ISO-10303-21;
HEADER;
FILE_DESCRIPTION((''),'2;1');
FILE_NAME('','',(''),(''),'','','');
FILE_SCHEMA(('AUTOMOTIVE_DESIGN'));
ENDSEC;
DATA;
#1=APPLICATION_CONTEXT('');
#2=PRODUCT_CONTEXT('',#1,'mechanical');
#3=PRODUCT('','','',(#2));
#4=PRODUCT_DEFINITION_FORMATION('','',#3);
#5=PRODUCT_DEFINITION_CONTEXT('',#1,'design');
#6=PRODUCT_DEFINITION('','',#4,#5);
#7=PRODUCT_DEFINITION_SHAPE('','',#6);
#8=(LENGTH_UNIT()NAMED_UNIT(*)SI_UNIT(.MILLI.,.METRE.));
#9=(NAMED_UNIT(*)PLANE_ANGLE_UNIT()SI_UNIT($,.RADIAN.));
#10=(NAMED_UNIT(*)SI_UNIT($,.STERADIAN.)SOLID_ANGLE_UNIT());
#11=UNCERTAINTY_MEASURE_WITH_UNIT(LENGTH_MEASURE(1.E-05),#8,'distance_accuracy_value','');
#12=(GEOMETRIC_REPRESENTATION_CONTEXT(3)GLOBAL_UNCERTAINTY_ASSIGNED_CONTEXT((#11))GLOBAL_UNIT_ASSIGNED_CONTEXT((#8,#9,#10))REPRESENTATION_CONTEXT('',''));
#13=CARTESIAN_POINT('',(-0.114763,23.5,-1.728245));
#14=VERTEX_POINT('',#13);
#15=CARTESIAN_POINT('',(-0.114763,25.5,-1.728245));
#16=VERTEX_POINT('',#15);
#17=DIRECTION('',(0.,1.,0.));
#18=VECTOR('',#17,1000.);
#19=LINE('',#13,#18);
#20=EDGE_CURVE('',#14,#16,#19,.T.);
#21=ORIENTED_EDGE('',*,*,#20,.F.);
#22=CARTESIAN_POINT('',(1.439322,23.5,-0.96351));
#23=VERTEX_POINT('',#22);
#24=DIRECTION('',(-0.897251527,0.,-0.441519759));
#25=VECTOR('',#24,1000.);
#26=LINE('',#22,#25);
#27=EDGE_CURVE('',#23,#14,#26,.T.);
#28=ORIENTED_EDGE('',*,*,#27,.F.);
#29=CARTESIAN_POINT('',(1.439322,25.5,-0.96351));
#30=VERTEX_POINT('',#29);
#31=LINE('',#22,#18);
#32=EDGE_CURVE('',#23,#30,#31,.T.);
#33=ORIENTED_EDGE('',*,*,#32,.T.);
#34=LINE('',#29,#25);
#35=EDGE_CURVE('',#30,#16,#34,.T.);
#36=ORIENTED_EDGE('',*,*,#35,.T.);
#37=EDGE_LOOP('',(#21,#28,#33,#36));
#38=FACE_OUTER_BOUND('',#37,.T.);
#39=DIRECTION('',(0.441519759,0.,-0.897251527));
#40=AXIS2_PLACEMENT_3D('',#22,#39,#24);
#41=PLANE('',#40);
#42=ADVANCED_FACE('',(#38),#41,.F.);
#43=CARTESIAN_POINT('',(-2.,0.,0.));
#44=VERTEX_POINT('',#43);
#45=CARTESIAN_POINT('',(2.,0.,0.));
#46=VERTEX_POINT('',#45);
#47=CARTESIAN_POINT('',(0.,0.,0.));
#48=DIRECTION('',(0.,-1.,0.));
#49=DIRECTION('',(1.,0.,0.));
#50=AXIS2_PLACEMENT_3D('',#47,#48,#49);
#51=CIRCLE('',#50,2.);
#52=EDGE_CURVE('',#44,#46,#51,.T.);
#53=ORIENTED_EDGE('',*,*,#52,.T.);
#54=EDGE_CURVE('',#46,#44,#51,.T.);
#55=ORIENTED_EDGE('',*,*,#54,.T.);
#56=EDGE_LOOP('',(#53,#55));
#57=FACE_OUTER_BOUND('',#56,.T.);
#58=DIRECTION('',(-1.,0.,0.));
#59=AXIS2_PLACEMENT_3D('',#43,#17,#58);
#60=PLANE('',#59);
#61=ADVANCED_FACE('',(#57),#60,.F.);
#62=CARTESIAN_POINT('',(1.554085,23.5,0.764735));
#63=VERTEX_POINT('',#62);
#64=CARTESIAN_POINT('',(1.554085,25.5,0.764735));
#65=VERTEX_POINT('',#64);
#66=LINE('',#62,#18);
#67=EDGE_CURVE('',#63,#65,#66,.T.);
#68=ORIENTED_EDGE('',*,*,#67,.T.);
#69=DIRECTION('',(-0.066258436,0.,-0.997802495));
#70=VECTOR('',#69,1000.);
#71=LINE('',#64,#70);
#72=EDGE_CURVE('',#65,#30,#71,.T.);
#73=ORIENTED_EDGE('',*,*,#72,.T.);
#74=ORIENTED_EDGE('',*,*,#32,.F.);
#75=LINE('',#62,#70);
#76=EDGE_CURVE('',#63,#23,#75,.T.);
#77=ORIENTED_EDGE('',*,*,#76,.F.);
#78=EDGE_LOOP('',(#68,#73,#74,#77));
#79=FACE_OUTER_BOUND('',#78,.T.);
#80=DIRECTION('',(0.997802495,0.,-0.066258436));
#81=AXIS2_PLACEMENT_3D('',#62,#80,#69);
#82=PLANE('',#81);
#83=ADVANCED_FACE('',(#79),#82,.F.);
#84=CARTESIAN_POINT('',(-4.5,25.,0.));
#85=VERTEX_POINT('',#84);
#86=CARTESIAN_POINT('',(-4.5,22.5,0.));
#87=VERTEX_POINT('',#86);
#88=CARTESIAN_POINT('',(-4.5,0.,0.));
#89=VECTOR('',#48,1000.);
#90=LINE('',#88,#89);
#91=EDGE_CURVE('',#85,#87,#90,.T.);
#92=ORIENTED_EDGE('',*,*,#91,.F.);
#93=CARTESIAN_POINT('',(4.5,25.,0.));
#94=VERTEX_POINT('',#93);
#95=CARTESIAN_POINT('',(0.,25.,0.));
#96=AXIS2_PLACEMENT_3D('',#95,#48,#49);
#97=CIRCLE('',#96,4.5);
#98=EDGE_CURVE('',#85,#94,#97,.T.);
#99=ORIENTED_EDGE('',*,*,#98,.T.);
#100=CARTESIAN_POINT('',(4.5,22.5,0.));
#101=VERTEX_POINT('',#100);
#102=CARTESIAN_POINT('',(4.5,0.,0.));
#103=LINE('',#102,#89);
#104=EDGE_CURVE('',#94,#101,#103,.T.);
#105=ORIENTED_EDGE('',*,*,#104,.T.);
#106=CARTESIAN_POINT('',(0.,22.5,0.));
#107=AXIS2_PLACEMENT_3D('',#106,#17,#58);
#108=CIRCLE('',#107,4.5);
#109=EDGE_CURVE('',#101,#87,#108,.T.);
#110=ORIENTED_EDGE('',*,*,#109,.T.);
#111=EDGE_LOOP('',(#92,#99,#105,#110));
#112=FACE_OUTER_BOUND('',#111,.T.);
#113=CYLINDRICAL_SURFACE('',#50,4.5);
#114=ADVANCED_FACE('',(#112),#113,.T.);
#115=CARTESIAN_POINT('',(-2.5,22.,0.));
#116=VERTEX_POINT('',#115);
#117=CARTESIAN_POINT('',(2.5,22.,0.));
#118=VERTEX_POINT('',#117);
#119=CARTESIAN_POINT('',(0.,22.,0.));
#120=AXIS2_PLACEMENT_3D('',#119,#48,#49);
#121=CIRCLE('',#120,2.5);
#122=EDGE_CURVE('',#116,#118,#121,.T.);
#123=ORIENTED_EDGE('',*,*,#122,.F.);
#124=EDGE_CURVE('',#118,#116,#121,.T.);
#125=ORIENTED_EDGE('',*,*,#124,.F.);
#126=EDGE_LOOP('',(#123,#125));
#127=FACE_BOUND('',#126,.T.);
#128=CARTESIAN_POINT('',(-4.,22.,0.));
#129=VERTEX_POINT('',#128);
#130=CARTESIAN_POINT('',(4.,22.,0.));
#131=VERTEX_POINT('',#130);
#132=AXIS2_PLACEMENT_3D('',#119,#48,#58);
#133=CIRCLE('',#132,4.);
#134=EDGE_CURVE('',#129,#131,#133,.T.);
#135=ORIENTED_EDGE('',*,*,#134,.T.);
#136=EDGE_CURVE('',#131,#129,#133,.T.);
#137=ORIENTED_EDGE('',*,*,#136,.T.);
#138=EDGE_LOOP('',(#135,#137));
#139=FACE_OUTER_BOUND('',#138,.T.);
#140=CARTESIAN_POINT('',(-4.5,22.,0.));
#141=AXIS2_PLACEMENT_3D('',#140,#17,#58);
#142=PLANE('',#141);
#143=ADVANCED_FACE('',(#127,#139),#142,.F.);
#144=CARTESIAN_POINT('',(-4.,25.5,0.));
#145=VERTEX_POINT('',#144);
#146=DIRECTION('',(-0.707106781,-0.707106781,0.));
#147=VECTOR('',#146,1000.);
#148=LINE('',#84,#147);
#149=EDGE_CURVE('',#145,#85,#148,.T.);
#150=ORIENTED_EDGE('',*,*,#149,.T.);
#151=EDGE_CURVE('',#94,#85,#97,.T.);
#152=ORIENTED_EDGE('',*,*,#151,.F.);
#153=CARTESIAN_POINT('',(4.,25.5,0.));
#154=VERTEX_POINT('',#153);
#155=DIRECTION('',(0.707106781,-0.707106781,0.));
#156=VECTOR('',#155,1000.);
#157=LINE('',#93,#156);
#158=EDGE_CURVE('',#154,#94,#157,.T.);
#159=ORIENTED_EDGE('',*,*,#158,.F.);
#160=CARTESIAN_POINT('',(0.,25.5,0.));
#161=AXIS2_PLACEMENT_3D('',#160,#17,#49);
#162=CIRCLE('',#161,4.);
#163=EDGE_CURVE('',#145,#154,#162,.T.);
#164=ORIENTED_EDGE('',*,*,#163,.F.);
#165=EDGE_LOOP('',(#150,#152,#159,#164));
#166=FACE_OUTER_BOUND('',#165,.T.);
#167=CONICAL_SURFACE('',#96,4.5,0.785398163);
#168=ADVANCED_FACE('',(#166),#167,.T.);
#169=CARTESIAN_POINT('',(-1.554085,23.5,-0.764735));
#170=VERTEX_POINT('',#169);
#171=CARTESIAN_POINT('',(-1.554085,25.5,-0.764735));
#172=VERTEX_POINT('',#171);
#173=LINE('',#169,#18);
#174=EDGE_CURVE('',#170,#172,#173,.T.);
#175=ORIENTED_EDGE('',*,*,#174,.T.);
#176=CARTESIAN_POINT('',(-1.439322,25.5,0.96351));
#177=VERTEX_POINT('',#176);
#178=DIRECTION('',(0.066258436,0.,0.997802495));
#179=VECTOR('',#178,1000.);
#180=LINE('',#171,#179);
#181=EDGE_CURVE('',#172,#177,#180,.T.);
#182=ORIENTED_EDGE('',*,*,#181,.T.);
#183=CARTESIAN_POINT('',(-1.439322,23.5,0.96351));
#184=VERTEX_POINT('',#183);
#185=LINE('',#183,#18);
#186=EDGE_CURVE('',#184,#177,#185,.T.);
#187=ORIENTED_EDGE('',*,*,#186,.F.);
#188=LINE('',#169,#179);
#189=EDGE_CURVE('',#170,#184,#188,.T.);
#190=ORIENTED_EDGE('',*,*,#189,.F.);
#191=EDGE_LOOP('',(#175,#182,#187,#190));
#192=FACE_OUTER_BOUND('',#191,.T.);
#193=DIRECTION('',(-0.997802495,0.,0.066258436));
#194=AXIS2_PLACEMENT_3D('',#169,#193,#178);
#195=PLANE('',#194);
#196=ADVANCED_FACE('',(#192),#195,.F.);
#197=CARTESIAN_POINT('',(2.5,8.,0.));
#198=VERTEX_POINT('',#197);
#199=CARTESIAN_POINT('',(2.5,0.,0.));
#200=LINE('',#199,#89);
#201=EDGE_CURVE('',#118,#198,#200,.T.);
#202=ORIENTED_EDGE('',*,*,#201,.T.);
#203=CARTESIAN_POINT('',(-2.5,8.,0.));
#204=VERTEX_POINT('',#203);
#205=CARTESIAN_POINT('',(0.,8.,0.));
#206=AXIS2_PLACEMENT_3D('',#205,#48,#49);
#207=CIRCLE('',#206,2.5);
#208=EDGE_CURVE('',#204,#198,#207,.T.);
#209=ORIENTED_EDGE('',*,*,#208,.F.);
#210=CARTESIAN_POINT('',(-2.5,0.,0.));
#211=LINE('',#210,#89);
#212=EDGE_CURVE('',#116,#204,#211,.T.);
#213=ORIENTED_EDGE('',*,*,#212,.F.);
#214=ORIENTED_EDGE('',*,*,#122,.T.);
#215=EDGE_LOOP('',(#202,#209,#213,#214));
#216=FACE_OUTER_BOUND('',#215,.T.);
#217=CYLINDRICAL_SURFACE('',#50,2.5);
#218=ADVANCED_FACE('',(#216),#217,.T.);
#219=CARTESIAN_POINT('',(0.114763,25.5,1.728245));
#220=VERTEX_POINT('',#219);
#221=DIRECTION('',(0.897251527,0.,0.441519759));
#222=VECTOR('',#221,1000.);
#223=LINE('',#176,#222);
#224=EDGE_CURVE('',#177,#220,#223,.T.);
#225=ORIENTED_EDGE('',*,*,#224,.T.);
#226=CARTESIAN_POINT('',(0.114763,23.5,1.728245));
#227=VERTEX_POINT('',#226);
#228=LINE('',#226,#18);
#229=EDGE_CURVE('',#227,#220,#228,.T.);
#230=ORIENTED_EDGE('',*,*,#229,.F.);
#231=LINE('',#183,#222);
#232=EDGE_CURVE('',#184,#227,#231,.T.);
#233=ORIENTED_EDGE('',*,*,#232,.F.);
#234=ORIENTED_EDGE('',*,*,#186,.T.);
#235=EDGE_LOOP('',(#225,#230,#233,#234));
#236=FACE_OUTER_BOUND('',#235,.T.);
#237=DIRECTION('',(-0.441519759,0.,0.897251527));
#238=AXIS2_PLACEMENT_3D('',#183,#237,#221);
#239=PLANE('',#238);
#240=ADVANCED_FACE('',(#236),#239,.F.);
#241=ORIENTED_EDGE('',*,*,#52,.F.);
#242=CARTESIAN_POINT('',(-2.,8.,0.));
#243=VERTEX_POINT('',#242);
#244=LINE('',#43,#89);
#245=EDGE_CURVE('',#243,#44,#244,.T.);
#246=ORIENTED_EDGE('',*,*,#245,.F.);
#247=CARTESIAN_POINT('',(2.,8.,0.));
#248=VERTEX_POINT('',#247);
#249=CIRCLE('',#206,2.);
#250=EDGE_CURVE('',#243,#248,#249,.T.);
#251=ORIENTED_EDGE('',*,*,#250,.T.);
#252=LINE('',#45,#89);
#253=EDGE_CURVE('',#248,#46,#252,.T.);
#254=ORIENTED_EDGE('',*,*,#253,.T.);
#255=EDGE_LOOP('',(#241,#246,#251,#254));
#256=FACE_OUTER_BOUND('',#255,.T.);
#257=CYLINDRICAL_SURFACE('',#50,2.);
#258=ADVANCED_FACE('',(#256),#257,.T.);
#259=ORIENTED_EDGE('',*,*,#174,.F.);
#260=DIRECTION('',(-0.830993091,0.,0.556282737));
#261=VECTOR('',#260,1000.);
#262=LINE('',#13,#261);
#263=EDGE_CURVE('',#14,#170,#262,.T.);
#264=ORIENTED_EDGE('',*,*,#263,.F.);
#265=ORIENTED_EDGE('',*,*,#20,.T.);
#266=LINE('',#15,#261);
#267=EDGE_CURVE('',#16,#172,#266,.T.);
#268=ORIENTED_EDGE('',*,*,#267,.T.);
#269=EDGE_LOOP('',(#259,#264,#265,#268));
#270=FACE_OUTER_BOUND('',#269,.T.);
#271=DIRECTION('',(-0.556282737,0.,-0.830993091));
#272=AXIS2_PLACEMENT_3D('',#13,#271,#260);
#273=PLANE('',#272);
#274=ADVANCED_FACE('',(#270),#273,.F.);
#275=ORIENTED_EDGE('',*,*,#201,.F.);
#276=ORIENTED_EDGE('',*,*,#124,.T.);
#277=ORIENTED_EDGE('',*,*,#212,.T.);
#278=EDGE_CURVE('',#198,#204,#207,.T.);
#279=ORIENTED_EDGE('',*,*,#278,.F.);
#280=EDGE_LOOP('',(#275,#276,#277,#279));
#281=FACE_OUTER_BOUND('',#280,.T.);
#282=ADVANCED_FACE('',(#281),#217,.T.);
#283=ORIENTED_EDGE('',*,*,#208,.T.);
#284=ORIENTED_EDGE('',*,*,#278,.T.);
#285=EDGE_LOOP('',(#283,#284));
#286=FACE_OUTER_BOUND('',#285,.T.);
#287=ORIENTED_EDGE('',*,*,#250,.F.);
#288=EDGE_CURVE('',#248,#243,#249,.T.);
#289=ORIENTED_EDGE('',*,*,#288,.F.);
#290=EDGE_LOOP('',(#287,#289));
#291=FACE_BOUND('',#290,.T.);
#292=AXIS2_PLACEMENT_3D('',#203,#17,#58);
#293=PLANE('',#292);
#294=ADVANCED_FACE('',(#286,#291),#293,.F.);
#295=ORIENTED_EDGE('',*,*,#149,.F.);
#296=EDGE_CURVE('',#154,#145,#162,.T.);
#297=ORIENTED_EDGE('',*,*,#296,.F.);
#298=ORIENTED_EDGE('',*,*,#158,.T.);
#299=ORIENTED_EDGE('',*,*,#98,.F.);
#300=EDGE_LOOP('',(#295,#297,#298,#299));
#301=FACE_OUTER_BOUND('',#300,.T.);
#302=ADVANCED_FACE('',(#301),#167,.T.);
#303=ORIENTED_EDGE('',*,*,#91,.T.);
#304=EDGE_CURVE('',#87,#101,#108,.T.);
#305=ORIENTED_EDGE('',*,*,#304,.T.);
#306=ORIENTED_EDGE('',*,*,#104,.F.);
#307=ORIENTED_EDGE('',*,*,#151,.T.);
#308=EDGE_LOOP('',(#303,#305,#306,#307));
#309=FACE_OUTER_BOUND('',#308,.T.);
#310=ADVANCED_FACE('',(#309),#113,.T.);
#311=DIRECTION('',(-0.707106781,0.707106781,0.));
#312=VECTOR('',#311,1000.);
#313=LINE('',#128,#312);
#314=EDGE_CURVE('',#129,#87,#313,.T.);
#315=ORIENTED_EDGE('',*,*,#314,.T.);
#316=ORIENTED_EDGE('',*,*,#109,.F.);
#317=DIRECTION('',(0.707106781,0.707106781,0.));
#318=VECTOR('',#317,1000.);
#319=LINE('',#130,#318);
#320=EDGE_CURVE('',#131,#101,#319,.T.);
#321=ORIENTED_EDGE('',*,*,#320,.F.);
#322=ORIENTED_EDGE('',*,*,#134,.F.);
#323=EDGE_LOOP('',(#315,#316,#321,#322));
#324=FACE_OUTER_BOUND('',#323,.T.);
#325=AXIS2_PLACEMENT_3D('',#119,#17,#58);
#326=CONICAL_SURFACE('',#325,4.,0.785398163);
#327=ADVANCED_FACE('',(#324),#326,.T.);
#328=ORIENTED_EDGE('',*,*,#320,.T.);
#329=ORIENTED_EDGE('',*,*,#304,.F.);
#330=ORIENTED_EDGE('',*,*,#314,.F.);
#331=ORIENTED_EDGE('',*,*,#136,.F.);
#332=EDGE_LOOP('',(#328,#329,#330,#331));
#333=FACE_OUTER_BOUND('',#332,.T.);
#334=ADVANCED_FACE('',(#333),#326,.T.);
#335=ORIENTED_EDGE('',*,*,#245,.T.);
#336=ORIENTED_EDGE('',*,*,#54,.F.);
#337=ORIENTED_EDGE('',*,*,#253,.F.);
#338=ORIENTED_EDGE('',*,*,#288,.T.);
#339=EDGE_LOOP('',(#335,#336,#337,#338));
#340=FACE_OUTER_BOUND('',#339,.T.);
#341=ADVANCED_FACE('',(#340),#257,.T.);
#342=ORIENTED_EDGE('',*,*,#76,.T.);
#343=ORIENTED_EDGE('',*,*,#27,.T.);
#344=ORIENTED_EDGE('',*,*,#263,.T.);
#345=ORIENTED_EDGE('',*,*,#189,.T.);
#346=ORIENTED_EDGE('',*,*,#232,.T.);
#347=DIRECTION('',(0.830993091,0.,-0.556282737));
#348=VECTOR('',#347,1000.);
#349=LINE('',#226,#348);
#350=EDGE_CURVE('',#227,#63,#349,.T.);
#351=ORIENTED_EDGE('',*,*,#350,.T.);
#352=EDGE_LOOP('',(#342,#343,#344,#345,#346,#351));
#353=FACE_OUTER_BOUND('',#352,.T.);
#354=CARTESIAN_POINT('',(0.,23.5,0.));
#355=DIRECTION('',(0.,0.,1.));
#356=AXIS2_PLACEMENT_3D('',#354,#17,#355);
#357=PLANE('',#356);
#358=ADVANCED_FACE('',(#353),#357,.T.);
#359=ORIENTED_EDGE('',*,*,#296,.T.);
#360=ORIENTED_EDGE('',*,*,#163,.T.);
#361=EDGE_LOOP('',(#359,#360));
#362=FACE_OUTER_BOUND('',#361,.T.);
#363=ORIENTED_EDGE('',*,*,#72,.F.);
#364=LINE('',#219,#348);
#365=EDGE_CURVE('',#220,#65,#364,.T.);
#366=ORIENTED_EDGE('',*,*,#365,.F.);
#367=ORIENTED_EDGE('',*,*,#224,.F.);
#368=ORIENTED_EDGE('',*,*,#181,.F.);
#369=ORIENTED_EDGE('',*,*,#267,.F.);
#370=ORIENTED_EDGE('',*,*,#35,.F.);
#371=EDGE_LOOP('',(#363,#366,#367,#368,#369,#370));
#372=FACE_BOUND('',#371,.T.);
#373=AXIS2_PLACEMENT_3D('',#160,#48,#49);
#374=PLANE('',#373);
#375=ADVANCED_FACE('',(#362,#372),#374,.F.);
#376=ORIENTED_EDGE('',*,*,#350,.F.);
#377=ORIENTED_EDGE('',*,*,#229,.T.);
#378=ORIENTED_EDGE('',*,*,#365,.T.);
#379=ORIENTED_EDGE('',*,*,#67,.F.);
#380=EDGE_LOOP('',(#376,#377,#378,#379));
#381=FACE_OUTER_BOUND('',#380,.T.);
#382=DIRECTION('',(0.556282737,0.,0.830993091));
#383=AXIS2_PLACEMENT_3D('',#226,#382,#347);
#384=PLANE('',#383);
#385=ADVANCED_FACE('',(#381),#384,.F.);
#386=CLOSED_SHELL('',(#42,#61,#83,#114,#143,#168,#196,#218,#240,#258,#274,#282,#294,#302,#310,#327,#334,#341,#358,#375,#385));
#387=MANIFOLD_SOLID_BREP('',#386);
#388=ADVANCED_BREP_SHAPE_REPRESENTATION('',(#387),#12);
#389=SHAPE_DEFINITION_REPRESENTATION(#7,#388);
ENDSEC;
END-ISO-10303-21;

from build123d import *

# Parameters (mm, degrees)
CUT_EXTRUDE1_DEPTH = 2
CHAMFER1_SIZE      = 0.5


with BuildPart() as part:
    # Sketch1 → Revolve1 (revolve)
    with BuildSketch(Plane.XY, mode=Mode.PRIVATE) as revolve1_sk:
        Polygon((0, 0), (0, 25.5), (-4.5, 25.5), (-4.5, 22), (-2.5, 22), (-2.5, 8), (-2, 8), (-2, 0), align=None)
    revolve(revolve1_sk.sketch.rotate(Axis((0, 0, 0), (0, 1, 0)), 180), axis=Axis((0, 0, 0), (0, 1, 0)))

    # Sketch2 → Cut-Extrude1 (cut)
    with BuildSketch(Plane(origin=(0, 25.5, 0), x_dir=(1, 0, 0), z_dir=(0, 1, 0))):
        Polygon((1.554085232, -0.764734655), (1.439322254, 0.963509963), (-0.114762978, 1.728244618), (-1.554085232, 0.764734655), (-1.439322254, -0.963509963), (0.114762978, -1.728244618), align=None)
    extrude(amount=-CUT_EXTRUDE1_DEPTH, mode=Mode.SUBTRACT)

    # Chamfer1
    chamfer1_edges = [part.edges().sort_by_distance(p)[0] for p in [
        (-4.5, 22, 0),
        (-4.5, 25.5, 0),
    ]]
    chamfer(chamfer1_edges, length=CHAMFER1_SIZE)


solid = part.part
